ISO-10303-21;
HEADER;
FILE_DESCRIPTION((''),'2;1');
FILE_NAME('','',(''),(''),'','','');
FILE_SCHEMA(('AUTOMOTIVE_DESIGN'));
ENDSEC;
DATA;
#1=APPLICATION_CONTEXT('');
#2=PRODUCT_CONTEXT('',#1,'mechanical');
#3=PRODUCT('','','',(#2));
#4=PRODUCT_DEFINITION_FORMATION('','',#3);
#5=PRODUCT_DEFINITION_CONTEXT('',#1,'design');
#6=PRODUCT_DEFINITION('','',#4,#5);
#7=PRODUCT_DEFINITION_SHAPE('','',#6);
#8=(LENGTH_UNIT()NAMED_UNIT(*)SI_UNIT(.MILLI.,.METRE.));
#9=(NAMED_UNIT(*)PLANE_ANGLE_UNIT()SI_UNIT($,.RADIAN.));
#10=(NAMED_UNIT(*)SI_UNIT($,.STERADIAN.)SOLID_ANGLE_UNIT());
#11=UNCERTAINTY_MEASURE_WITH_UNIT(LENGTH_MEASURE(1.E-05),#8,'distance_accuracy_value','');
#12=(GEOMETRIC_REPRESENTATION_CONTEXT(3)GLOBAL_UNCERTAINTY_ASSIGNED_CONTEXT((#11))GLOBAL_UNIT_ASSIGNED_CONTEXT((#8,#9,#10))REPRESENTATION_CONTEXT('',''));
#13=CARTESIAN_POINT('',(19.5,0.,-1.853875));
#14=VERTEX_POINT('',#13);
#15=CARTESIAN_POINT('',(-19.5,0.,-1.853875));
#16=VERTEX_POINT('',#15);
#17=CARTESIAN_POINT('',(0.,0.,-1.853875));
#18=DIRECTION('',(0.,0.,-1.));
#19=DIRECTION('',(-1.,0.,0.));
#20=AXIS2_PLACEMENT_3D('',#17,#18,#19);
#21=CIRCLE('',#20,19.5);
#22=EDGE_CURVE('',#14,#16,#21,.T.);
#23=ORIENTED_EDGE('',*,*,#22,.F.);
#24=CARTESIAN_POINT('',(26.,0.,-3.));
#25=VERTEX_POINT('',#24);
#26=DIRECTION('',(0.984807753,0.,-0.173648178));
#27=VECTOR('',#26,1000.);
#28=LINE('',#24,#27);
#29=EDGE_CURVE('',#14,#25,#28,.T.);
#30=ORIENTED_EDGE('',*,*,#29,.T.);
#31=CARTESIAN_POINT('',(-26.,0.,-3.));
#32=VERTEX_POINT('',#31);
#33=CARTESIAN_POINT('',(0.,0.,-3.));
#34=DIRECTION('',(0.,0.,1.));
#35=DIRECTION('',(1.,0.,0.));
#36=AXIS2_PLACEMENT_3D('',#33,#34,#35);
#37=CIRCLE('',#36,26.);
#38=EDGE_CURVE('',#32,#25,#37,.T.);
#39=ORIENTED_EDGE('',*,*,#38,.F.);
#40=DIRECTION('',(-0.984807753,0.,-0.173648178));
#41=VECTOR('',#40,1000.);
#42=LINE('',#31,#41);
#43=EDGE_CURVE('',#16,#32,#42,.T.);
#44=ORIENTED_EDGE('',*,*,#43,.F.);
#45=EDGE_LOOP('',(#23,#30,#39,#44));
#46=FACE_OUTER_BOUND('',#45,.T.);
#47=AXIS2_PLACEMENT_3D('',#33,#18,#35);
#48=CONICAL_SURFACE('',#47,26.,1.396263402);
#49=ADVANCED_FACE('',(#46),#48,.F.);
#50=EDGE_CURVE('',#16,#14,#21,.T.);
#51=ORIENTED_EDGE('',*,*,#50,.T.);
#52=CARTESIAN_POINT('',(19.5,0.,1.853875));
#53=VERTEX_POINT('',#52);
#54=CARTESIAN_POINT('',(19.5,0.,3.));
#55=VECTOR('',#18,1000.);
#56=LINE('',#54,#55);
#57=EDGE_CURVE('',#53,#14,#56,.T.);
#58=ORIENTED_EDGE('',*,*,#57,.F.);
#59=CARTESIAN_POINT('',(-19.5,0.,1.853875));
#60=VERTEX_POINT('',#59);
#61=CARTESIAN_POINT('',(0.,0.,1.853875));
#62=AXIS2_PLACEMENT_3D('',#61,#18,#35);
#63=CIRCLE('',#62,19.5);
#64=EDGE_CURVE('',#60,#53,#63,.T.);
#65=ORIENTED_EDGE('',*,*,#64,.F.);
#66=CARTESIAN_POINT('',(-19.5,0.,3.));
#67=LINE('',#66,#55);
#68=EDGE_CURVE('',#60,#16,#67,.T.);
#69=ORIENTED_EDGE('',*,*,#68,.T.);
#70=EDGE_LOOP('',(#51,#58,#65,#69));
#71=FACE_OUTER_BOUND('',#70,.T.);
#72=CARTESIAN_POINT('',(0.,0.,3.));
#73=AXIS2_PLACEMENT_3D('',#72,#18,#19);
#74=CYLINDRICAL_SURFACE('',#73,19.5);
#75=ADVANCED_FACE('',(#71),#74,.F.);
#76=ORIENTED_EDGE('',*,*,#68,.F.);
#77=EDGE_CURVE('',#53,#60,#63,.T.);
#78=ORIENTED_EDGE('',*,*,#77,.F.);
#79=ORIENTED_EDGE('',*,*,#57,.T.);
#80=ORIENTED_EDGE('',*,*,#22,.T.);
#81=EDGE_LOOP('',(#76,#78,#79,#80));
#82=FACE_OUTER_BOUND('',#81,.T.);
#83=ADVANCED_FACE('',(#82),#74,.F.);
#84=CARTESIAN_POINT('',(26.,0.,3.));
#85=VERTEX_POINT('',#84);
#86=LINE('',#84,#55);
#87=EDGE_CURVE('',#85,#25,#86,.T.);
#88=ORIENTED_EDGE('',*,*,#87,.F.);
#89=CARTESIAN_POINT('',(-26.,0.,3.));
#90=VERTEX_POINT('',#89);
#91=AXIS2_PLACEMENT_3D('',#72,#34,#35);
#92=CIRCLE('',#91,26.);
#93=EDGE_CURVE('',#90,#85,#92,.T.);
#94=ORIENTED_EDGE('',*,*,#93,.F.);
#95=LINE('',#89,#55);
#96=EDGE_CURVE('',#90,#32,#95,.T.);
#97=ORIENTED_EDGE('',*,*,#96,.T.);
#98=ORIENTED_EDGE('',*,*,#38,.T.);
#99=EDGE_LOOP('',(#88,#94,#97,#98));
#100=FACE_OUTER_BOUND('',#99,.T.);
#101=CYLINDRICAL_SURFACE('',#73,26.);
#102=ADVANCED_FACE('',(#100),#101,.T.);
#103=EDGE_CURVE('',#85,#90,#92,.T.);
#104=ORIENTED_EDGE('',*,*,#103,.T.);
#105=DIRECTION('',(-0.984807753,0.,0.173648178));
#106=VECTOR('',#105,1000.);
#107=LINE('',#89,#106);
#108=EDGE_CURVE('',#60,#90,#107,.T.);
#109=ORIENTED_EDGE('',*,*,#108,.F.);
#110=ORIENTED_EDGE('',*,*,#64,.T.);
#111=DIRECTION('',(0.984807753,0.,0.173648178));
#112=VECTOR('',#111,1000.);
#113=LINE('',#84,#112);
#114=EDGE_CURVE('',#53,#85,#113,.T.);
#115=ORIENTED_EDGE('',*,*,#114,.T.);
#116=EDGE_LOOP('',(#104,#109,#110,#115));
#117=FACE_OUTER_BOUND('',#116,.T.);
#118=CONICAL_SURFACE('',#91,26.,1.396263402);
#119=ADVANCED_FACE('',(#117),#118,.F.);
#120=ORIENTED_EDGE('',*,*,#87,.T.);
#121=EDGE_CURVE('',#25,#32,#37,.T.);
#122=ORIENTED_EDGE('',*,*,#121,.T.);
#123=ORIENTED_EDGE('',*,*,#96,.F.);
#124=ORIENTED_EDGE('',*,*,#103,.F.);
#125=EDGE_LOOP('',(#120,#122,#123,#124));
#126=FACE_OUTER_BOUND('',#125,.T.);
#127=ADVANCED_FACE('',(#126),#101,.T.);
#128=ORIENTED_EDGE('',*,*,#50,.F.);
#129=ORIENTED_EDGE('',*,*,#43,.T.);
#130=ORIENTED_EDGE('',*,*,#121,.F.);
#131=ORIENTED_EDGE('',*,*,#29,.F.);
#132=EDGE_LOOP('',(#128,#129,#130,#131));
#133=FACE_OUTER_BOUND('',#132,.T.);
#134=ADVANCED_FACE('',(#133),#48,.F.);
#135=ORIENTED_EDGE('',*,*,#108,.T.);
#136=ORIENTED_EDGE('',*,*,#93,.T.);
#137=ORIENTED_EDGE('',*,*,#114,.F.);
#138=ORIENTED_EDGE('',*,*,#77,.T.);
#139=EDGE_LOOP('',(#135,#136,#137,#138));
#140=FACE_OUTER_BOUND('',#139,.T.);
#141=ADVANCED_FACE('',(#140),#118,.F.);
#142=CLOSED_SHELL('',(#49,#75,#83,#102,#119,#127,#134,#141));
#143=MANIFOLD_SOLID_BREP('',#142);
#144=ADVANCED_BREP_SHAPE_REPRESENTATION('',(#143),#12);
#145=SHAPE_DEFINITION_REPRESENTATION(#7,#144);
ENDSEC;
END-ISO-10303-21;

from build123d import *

# Parameters (mm, degrees)
SKETCH1_R           = 26
SKETCH1_R_2         = 19.5
BOSS_EXTRUDE1_DEPTH = 3


with BuildPart() as part:
    # Sketch1 → Boss-Extrude1 (new, symmetric)
    with BuildSketch(Plane.XY):
        Circle(SKETCH1_R)
        Circle(SKETCH1_R_2, mode=Mode.SUBTRACT)
    extrude(amount=BOSS_EXTRUDE1_DEPTH, both=True)

    # Cut-Extrude1 cone 1 section (through the dimple's axis) → Cut-Extrude1 (revolve, cut)
    with BuildSketch(Plane(origin=(0, 0, 3), x_dir=(0, -1, 0), z_dir=(1, 0, 0))):
        Polygon((0, 0), (26, 0), (0, 4.584501498), align=None)
    cut_extrude1 = revolve(axis=Axis((0, 0, 3), (0, 0, -1)), mode=Mode.SUBTRACT)

    # Mirror1: Cut-Extrude1 across plane
    add(cut_extrude1.mirror(Plane.XY), mode=Mode.SUBTRACT)


solid = part.part
